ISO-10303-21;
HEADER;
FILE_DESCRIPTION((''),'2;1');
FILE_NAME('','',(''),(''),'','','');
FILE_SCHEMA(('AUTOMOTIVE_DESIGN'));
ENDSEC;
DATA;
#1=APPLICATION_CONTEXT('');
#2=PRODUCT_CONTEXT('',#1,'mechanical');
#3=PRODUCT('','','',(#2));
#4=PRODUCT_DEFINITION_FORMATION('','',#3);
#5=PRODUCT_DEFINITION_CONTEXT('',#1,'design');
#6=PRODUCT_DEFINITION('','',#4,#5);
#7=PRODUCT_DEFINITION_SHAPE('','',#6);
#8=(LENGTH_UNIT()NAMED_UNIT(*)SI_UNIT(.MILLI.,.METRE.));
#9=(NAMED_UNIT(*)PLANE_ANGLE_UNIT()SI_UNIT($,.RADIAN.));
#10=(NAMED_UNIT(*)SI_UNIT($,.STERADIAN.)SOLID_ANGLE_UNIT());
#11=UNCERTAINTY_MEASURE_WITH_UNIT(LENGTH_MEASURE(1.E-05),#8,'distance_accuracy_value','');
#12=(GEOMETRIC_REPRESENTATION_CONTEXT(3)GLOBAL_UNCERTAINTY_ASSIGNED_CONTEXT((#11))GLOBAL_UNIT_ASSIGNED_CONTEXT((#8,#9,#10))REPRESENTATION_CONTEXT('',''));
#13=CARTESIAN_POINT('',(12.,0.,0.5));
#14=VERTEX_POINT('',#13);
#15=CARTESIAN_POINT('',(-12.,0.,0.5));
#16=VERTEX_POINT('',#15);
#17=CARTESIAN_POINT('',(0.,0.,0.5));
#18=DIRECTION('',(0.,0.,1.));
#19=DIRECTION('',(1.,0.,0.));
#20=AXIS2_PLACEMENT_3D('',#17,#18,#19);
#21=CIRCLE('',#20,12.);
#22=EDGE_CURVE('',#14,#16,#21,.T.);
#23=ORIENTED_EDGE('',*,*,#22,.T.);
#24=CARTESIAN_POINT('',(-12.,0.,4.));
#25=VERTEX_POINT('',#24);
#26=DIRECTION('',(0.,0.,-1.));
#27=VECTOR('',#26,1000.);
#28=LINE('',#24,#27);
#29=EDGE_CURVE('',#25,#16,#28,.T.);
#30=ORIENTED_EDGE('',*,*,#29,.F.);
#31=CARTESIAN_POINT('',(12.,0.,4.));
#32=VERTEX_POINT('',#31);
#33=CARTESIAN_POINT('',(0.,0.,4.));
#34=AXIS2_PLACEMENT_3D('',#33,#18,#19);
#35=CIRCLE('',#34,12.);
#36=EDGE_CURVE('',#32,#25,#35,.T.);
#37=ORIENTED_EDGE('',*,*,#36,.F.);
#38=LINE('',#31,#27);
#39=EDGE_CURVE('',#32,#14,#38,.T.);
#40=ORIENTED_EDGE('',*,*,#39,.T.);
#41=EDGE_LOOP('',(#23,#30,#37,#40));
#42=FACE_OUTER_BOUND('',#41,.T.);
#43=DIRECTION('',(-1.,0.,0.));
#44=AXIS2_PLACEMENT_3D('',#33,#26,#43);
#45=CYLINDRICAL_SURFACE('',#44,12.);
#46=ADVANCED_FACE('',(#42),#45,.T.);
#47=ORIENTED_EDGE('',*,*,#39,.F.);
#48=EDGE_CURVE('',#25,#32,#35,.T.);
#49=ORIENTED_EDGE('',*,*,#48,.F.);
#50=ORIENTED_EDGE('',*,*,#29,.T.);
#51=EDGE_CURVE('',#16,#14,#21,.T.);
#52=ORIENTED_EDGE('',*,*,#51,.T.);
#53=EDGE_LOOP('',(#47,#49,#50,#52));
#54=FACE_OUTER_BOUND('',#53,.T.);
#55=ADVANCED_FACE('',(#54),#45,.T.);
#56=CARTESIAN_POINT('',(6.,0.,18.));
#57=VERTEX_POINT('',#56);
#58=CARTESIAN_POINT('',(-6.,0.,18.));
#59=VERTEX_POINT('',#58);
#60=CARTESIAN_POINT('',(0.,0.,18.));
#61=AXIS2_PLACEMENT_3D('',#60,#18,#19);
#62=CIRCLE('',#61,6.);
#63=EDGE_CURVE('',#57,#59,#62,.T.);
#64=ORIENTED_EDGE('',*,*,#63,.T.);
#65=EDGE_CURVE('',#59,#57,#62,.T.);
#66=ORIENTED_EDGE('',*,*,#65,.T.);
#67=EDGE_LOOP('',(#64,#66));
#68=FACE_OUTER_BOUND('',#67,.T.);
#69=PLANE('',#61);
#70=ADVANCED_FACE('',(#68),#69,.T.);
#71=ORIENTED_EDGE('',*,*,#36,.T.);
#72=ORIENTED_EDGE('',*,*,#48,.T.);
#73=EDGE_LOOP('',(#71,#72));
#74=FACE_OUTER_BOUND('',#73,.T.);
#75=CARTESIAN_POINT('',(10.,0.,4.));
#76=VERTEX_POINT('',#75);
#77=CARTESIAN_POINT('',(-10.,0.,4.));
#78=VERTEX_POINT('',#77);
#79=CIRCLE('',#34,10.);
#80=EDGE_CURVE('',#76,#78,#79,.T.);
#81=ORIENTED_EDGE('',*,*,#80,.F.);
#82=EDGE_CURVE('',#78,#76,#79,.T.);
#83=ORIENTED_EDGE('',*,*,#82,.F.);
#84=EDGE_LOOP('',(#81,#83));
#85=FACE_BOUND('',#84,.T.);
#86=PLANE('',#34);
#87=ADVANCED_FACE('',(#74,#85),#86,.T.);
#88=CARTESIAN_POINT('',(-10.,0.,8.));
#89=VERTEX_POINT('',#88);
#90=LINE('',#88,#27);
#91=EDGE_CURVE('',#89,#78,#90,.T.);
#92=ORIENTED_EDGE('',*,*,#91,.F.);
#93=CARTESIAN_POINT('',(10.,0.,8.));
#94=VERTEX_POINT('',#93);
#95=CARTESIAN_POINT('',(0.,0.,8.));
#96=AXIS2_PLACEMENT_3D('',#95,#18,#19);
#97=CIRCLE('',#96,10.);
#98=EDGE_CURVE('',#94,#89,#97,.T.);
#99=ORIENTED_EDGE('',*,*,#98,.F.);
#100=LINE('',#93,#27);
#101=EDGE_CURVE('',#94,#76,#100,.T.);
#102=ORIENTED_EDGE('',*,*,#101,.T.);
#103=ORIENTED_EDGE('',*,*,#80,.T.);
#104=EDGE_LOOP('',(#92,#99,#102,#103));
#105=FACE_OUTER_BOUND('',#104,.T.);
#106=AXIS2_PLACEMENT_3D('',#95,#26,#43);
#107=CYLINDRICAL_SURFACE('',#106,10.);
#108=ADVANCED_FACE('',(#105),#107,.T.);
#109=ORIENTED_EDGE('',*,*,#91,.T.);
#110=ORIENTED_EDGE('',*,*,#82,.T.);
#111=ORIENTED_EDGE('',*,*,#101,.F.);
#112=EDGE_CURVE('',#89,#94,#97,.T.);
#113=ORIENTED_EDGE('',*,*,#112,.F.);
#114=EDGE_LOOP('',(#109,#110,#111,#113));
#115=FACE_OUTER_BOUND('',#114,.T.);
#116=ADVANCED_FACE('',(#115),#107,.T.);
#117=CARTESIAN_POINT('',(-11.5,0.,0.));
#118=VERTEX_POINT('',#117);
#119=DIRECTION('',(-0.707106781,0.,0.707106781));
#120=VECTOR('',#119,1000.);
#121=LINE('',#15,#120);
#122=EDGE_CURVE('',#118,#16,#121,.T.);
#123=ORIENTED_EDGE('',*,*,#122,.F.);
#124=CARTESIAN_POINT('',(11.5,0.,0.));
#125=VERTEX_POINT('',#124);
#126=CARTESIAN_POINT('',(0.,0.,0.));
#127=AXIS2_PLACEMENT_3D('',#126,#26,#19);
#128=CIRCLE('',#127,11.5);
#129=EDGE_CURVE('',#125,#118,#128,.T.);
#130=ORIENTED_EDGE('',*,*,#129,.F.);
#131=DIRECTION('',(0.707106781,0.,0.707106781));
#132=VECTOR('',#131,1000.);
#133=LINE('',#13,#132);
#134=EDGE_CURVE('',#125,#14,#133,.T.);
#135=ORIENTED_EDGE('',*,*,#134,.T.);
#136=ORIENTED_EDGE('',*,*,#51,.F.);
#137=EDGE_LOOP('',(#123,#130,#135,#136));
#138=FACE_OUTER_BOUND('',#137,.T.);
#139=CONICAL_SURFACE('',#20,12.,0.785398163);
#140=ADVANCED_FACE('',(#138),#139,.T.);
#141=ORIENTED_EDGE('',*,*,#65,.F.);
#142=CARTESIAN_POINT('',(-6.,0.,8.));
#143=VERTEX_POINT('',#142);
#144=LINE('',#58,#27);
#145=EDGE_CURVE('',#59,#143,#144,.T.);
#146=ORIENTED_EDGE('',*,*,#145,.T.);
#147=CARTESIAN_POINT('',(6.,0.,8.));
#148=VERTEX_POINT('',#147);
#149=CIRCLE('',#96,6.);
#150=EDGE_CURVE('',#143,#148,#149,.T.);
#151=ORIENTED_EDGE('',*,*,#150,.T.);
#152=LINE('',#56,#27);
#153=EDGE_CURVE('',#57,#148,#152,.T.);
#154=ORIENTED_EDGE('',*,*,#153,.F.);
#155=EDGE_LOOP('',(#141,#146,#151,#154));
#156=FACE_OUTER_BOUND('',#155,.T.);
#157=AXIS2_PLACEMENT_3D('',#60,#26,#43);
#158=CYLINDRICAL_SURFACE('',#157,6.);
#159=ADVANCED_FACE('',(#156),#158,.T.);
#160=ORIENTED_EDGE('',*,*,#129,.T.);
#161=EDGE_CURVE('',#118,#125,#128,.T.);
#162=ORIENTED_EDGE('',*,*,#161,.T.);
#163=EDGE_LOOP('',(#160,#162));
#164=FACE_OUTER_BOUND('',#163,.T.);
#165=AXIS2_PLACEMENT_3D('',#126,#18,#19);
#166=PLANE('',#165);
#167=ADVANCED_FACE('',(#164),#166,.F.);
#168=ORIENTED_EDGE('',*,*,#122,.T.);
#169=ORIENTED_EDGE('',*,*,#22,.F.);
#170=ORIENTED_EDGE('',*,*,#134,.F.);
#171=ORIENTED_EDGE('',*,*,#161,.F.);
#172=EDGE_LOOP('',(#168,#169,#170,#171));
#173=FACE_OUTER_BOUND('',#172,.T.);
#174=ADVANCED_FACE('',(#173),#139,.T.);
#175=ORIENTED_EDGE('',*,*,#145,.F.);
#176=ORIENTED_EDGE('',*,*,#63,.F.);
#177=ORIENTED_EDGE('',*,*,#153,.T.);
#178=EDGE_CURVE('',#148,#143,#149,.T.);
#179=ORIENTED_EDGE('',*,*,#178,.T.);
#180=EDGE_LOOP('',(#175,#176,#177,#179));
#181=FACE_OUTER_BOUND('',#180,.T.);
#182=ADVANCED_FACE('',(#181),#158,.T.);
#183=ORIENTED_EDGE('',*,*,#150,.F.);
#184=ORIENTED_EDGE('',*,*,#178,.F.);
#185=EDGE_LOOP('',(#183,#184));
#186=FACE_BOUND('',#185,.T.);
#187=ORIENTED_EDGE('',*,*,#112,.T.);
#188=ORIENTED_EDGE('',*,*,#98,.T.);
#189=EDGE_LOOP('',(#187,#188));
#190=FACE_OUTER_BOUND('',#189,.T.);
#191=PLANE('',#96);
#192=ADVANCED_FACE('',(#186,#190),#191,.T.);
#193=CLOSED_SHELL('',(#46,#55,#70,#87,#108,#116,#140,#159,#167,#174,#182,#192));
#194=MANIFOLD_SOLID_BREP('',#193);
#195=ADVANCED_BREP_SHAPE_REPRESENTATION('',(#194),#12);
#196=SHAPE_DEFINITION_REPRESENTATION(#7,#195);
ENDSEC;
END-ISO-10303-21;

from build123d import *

# Parameters (mm, degrees)
SKETCH_1_4_R        = 6
BOSS_EXTRUDE1_DEPTH = 18
SKETCH_1_3_R        = 10
SKETCH_1_3_R_2      = 6
BOSS_EXTRUDE2_DEPTH = 8
SKETCH_1_4_2_R      = 12
SKETCH_1_4_2_R_2    = 10
BOSS_EXTRUDE3_DEPTH = 4
CHAMFER1_SIZE       = 0.5


with BuildPart() as part:
    # Sketch 1_4 → Boss-Extrude1 (new body)
    with BuildSketch(Plane.XY):
        Circle(SKETCH_1_4_R)
    extrude(amount=BOSS_EXTRUDE1_DEPTH)

    # 草图1<3> → Boss-Extrude2 (add)
    with BuildSketch(Plane.XY):
        Circle(SKETCH_1_3_R)
        Circle(SKETCH_1_3_R_2, mode=Mode.SUBTRACT)
    extrude(amount=BOSS_EXTRUDE2_DEPTH)

    # Sketch 1_4 2 → Boss-Extrude3 (add)
    with BuildSketch(Plane.XY):
        Circle(SKETCH_1_4_2_R)
        Circle(SKETCH_1_4_2_R_2, mode=Mode.SUBTRACT)
    extrude(amount=BOSS_EXTRUDE3_DEPTH)

    # Chamfer1
    chamfer1_edges = [part.edges().sort_by_distance(p)[0] for p in [
        (-12, 0, 0),
    ]]
    chamfer(chamfer1_edges, length=CHAMFER1_SIZE)


solid = part.part
